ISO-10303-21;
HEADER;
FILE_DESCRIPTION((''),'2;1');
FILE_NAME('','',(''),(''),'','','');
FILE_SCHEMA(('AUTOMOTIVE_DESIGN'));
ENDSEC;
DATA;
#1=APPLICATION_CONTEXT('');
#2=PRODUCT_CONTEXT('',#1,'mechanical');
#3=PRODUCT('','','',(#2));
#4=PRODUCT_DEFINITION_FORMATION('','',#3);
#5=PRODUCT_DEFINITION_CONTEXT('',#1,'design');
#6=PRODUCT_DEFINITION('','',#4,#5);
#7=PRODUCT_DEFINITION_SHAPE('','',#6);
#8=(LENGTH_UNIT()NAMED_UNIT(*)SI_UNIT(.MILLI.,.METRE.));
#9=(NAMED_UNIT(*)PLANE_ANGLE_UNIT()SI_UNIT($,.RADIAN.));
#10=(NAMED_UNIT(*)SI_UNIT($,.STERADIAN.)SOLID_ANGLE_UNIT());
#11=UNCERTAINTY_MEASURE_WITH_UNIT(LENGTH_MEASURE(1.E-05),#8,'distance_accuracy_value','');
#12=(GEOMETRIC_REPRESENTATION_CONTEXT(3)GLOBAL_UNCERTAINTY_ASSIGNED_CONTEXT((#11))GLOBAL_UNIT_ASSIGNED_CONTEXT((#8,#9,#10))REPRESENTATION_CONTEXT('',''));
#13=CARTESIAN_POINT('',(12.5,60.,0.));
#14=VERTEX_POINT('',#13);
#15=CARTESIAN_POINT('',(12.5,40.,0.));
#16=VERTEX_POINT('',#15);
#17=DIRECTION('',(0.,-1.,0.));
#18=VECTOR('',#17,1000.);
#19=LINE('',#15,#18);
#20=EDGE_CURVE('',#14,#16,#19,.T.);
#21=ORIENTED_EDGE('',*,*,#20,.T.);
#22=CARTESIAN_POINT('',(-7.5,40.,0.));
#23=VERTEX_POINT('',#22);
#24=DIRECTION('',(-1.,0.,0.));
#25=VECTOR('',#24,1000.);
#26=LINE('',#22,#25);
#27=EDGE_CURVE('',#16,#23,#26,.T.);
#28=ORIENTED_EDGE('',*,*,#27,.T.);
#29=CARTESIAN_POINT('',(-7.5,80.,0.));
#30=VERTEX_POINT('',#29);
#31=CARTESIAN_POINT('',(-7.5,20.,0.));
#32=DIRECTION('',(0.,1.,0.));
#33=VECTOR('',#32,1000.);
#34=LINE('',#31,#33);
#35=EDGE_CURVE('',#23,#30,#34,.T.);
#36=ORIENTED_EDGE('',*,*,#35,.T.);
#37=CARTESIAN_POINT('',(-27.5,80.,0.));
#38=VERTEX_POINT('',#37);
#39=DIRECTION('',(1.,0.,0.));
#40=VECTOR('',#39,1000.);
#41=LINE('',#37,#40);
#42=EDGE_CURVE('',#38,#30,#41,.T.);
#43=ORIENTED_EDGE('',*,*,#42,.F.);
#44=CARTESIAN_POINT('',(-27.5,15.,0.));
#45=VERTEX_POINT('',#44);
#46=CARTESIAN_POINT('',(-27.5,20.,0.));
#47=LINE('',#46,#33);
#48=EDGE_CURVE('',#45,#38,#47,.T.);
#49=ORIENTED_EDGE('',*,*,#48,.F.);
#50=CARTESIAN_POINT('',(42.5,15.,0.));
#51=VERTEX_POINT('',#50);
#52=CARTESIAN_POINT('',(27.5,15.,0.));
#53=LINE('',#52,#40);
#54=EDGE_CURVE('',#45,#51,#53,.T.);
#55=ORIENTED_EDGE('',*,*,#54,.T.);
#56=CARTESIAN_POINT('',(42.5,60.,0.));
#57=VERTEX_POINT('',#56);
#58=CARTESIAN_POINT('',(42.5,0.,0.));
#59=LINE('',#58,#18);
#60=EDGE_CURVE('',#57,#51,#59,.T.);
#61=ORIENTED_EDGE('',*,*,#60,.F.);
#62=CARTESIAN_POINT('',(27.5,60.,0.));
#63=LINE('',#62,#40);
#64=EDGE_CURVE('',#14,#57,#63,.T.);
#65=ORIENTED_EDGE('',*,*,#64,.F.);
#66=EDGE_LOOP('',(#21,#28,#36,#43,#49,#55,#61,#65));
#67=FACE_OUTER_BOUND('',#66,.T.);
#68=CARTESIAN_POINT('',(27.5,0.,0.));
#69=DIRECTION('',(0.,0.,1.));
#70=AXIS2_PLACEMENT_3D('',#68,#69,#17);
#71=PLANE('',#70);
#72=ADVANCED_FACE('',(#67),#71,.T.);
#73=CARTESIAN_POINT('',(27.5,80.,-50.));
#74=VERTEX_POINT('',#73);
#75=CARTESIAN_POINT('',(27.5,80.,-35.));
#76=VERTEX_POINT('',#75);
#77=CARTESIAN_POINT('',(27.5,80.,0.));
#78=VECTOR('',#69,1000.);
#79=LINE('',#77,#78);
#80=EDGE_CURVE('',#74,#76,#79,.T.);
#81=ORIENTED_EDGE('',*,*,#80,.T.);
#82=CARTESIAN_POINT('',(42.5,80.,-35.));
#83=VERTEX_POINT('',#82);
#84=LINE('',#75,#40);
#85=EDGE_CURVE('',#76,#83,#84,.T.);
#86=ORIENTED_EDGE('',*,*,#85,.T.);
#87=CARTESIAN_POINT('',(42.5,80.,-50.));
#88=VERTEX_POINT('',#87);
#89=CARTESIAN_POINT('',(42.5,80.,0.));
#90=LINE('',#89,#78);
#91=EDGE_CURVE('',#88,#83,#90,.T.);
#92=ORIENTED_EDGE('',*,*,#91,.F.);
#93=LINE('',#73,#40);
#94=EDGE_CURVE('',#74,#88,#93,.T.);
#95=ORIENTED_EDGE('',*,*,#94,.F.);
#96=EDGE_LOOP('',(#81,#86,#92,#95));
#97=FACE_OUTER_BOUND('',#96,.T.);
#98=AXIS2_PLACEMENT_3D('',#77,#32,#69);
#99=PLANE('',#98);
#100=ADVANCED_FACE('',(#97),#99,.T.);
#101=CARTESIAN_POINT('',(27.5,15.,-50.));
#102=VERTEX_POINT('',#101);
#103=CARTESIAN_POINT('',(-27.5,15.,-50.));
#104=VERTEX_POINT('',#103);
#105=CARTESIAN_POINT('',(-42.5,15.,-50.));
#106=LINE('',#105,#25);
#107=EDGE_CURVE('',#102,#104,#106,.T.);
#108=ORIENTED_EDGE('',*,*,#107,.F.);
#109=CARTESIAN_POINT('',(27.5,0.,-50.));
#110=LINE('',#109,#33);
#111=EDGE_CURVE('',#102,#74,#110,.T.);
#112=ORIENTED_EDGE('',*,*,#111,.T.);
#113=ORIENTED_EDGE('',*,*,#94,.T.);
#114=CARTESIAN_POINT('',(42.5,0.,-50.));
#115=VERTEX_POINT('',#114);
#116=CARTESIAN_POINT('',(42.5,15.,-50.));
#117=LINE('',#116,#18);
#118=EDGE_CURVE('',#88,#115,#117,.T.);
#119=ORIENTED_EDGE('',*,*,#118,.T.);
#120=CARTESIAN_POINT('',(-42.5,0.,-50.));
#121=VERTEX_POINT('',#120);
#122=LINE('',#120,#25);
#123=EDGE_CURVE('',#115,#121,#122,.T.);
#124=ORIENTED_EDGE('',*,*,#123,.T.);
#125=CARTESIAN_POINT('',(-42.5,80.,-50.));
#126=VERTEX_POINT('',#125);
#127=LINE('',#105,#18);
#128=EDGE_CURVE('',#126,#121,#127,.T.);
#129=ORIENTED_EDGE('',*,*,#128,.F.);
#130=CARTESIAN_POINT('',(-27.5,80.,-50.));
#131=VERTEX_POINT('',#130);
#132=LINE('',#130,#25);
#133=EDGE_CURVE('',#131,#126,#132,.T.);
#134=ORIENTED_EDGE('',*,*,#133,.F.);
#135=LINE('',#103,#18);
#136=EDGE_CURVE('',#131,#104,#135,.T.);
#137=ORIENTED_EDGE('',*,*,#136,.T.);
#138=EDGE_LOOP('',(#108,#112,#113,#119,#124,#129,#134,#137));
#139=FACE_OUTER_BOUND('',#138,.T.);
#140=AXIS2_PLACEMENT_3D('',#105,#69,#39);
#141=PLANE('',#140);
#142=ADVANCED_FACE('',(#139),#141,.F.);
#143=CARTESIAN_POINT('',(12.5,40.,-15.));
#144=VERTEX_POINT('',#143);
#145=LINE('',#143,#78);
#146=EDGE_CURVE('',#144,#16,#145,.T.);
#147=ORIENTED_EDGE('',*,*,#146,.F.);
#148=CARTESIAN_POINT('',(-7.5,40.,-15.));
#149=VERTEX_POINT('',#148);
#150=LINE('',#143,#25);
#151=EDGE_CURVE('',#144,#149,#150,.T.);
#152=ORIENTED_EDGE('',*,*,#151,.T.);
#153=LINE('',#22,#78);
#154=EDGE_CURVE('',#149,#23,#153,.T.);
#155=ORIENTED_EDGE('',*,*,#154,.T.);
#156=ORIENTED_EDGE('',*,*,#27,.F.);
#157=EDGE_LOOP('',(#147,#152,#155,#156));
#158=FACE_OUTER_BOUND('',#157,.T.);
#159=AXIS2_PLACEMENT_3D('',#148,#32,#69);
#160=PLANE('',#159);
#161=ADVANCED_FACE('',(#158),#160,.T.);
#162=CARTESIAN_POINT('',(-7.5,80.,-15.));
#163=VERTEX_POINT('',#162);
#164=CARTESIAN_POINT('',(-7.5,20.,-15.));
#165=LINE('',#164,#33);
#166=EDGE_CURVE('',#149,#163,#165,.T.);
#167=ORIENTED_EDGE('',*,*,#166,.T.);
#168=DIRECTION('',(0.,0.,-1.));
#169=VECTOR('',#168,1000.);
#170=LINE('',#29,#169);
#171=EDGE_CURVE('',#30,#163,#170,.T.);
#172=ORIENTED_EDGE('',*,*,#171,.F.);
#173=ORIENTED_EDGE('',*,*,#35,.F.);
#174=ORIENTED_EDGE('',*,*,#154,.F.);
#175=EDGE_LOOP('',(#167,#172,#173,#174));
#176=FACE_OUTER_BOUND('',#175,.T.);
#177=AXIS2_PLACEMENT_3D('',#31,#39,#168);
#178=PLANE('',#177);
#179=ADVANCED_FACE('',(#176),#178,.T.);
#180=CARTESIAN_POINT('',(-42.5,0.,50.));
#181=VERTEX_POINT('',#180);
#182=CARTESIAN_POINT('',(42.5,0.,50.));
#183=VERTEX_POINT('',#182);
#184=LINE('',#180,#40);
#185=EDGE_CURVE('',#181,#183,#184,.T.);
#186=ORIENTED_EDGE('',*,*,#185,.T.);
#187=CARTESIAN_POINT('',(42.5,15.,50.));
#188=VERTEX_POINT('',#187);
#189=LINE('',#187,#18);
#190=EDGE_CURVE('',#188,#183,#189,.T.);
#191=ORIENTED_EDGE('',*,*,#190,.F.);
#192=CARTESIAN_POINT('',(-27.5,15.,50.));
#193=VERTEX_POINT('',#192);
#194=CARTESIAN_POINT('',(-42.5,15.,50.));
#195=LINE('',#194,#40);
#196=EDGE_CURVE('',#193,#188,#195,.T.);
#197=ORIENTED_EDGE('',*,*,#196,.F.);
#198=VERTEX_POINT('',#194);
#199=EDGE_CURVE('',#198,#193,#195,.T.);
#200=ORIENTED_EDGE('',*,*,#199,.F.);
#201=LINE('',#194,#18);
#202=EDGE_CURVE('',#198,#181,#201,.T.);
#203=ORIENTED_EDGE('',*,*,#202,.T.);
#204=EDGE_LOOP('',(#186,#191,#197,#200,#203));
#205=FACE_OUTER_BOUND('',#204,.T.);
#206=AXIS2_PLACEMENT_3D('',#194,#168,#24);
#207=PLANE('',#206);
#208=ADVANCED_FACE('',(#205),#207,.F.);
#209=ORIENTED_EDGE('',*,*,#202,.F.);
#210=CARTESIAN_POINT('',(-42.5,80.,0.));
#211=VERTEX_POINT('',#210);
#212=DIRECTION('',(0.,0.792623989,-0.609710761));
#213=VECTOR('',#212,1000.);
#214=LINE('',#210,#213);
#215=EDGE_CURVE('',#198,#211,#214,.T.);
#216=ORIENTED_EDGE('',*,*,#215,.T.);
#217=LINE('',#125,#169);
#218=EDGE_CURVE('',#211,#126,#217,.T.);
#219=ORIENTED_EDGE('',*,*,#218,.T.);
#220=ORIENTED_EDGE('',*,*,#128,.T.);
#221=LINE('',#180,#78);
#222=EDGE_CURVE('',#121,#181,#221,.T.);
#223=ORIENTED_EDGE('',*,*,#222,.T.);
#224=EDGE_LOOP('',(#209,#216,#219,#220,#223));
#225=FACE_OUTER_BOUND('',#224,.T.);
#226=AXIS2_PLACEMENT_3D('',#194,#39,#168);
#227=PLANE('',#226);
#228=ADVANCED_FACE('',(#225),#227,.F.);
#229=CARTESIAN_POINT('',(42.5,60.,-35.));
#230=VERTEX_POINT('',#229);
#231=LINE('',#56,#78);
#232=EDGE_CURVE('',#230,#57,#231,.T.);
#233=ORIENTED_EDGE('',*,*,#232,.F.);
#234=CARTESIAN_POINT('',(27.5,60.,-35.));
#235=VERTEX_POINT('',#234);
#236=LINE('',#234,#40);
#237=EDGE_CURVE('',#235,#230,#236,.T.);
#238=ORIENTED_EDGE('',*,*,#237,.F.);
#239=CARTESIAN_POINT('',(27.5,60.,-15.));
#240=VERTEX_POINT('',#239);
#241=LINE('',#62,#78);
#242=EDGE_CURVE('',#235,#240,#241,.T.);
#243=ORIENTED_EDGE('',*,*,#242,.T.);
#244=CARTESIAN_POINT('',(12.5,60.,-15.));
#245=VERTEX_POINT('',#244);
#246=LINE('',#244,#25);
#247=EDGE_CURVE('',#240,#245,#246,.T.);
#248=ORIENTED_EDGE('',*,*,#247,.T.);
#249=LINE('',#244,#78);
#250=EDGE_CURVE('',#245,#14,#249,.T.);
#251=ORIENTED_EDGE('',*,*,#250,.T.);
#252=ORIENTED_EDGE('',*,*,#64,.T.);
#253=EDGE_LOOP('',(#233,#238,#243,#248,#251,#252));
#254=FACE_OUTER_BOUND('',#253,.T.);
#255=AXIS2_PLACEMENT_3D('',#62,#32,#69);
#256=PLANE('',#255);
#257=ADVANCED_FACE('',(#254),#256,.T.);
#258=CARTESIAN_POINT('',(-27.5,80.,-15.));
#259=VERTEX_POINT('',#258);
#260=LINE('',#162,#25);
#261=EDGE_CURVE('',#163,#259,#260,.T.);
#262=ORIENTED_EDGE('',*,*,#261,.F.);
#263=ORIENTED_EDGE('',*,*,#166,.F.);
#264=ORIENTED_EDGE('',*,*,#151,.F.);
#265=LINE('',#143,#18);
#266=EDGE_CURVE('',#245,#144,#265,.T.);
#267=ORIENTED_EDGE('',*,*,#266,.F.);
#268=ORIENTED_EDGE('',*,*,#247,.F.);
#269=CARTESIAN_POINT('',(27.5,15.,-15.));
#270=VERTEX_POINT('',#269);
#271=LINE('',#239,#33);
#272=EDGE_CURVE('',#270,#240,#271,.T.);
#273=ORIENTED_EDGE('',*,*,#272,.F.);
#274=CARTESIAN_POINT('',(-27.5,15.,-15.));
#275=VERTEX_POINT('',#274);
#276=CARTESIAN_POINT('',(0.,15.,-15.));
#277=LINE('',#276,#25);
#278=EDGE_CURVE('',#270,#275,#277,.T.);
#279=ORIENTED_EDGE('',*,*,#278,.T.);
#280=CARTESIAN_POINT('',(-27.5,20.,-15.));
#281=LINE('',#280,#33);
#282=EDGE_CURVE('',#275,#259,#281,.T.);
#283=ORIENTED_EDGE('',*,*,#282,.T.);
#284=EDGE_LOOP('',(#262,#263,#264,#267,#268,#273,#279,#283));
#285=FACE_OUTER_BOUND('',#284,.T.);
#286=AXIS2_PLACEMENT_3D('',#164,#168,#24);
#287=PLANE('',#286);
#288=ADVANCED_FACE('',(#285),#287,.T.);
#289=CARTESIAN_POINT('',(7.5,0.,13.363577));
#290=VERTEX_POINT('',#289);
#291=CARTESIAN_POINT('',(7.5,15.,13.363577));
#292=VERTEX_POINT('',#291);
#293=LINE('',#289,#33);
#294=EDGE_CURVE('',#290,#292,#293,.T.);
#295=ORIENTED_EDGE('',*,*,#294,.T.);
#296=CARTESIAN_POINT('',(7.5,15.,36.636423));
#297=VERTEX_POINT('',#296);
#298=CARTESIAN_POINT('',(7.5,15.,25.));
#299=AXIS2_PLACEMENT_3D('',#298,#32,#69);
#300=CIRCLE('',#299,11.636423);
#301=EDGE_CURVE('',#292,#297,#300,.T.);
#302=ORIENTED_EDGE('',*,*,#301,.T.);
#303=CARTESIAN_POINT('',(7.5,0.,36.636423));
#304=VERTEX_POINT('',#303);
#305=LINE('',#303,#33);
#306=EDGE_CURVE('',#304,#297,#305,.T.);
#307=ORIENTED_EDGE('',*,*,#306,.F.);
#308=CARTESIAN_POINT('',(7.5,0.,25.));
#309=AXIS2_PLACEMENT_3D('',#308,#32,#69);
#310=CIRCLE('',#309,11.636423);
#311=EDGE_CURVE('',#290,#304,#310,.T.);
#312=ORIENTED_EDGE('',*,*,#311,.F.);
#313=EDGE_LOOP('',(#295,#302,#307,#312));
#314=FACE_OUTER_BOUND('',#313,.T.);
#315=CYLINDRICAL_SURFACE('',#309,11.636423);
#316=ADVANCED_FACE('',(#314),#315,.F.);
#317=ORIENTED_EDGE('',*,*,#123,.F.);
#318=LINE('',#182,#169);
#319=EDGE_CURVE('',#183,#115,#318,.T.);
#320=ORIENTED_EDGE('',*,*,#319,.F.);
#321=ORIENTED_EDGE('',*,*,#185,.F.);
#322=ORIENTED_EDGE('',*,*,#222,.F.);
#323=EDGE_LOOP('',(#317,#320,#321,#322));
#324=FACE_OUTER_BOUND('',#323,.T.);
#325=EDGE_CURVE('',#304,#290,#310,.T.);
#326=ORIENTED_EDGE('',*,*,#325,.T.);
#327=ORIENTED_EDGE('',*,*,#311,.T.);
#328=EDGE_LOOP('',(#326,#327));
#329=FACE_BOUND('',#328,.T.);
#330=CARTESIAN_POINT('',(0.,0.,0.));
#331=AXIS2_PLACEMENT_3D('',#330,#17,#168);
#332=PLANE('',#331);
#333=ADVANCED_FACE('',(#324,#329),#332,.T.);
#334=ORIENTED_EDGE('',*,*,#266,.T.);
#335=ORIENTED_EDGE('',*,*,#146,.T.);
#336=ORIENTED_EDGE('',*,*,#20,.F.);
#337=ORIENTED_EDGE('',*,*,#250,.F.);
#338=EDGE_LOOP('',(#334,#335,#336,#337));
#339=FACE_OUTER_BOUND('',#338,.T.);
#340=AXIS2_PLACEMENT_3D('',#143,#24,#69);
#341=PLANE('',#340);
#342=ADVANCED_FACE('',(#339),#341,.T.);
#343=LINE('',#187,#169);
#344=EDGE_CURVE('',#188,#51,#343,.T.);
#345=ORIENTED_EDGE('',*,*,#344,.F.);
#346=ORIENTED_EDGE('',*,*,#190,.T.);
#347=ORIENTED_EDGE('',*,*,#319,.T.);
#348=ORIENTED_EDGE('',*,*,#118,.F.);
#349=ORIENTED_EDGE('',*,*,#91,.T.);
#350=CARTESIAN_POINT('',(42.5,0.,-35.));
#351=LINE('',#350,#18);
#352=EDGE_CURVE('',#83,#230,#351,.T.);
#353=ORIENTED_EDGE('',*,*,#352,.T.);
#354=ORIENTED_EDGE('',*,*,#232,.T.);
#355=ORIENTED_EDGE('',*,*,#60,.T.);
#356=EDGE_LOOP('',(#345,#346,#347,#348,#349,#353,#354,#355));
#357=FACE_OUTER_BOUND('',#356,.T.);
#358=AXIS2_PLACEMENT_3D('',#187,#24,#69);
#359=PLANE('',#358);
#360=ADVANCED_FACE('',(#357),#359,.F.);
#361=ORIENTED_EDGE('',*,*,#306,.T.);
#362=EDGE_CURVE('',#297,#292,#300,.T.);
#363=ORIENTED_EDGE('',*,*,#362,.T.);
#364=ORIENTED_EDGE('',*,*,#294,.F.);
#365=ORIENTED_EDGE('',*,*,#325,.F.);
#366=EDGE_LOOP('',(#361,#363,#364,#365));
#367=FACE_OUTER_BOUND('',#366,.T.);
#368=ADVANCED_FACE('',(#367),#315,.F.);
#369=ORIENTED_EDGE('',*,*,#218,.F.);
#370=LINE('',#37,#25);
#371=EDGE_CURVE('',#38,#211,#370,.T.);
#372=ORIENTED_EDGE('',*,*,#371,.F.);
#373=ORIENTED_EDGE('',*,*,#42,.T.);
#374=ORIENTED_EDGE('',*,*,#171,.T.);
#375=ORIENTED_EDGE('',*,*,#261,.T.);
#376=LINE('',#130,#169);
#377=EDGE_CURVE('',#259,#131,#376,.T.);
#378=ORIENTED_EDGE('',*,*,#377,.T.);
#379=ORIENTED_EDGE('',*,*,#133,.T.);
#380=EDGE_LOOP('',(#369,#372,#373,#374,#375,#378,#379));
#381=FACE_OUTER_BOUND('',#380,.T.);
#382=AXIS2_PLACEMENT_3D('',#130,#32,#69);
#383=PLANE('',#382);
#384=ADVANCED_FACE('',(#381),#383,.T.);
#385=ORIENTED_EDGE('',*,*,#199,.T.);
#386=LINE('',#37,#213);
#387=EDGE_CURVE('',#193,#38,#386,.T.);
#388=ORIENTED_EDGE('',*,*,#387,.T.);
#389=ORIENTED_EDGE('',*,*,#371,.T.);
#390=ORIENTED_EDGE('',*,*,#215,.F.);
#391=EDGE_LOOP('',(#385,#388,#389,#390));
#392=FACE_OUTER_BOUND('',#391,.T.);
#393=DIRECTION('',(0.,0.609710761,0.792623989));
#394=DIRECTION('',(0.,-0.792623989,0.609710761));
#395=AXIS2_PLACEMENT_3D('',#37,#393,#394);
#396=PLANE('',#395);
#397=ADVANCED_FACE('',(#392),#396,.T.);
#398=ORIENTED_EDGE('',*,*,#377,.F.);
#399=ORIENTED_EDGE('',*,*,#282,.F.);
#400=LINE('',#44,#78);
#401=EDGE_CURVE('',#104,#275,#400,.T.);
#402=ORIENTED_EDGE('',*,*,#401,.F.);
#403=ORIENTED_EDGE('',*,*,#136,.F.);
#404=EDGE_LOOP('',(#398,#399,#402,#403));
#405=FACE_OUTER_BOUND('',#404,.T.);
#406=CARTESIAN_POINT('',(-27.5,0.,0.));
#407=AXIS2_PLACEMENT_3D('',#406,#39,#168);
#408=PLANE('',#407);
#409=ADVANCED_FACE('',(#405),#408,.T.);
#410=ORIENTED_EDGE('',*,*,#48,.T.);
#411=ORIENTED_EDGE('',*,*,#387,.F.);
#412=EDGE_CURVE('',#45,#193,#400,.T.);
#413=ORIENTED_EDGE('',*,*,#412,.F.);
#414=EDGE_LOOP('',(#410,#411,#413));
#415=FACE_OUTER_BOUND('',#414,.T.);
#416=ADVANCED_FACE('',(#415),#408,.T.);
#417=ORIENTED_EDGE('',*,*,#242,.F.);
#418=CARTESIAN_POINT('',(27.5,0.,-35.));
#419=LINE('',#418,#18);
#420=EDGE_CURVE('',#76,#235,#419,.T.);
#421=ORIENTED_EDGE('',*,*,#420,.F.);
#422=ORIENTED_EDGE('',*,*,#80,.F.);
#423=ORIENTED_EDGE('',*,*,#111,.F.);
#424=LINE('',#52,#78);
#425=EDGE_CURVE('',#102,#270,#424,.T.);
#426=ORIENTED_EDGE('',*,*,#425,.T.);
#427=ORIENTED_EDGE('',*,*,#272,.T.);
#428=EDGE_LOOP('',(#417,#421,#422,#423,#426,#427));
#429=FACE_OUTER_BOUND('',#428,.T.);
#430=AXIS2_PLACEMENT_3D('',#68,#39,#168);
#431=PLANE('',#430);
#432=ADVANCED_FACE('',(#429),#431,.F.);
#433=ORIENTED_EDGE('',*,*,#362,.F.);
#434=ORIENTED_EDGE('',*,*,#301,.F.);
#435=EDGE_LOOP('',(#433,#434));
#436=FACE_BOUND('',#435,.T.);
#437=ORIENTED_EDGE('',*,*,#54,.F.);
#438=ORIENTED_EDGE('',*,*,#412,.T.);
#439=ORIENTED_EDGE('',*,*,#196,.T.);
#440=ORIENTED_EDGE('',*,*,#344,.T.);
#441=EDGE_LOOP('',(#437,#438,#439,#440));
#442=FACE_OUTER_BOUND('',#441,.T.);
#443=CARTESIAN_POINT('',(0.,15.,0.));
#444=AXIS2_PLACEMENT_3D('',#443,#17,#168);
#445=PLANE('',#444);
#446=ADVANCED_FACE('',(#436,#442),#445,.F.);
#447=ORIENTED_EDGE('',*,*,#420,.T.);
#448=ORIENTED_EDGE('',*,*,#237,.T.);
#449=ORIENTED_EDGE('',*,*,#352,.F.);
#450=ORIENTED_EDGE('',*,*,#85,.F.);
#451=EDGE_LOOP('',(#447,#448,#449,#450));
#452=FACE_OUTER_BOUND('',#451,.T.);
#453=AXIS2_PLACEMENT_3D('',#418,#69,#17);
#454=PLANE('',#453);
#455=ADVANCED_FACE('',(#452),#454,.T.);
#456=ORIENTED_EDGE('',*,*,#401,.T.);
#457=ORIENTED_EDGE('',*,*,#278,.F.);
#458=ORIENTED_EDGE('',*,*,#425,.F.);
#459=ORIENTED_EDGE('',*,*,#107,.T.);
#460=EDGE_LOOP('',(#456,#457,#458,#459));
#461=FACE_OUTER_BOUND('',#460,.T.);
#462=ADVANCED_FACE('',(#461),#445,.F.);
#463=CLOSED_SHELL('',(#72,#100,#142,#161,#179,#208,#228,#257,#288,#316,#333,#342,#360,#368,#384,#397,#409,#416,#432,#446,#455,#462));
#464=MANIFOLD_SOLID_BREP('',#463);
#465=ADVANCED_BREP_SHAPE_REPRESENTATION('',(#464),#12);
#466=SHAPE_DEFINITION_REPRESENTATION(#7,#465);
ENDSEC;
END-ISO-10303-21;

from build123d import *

# Parameters (mm, degrees)
BASE_PLATE_SKETCH_W    = 85
BASE_PLATE_SKETCH_H    = 100
BASE_PLATE_DEPTH       = 15
UPRIGHT_WALL_DEPTH     = 15
SIDE_WALL_SKETCH_W     = 50
SIDE_WALL_SKETCH_H     = 65
SIDE_WALL_DEPTH        = 15
GUSSET_DEPTH           = 15
POST_SKETCH_W          = 20
POST_SKETCH_H          = 15
POST_DEPTH             = 60
STEPPED_BLOCK_DEPTH    = 15
MOUNTING_HOLE_SKETCH_R = 11.636423048
MOUNTING_HOLE_DEPTH    = 15


with BuildPart() as part:
    # Base Plate Sketch → Base Plate (new body)
    with BuildSketch(Plane(origin=(0, 0, 0), x_dir=(1, 0, 0), z_dir=(0, 1, 0))):
        Rectangle(BASE_PLATE_SKETCH_W, BASE_PLATE_SKETCH_H)
    extrude(amount=BASE_PLATE_DEPTH)

    # Upright Wall Sketch → Upright Wall (add)
    with BuildSketch(Plane(origin=(42.5, 0, 0), x_dir=(0, 0, -1), z_dir=(1, 0, 0))):
        Polygon((0, 15), (50, 15), (50, 80), (35, 80), (35, 60), (0, 60), align=None)
    extrude(amount=-UPRIGHT_WALL_DEPTH)

    # Side Wall Sketch → Side Wall (add)
    with BuildSketch(Plane.ZY.offset(42.5)):
        with Locations((-25, 47.5)):
            Rectangle(SIDE_WALL_SKETCH_W, SIDE_WALL_SKETCH_H)
    extrude(amount=-SIDE_WALL_DEPTH)

    # Gusset Sketch → Gusset (add)
    with BuildSketch(Plane.ZY.offset(42.5)):
        Polygon((0, 80), (50, 15), (0, 15), align=None)
    extrude(amount=-GUSSET_DEPTH)

    # Post Sketch → Post (add)
    with BuildSketch(Plane(origin=(0, 80, 0), x_dir=(1, 0, 0), z_dir=(0, 1, 0))):
        with Locations((-17.5, 7.5)):
            Rectangle(POST_SKETCH_W, POST_SKETCH_H)
    extrude(amount=-POST_DEPTH)

    # Stepped Block Sketch → Stepped Block (add)
    with BuildSketch(Plane.XY):
        Polygon((12.5, 40), (12.5, 60), (27.5, 60), (27.5, 15), (-7.5, 15), (-27.5, 14.790865335), (-27.5, 40), (-7.5, 40), align=None)
    extrude(amount=-STEPPED_BLOCK_DEPTH)

    # Mounting Hole Sketch → Mounting Hole (cut)
    with BuildSketch(Plane(origin=(0, 15, 0), x_dir=(1, 0, 0), z_dir=(0, 1, 0))):
        with Locations(Location((7.5, -25, 0), (0, 0, 270))):
            Circle(MOUNTING_HOLE_SKETCH_R)
    extrude(amount=-MOUNTING_HOLE_DEPTH, mode=Mode.SUBTRACT)


solid = part.part
